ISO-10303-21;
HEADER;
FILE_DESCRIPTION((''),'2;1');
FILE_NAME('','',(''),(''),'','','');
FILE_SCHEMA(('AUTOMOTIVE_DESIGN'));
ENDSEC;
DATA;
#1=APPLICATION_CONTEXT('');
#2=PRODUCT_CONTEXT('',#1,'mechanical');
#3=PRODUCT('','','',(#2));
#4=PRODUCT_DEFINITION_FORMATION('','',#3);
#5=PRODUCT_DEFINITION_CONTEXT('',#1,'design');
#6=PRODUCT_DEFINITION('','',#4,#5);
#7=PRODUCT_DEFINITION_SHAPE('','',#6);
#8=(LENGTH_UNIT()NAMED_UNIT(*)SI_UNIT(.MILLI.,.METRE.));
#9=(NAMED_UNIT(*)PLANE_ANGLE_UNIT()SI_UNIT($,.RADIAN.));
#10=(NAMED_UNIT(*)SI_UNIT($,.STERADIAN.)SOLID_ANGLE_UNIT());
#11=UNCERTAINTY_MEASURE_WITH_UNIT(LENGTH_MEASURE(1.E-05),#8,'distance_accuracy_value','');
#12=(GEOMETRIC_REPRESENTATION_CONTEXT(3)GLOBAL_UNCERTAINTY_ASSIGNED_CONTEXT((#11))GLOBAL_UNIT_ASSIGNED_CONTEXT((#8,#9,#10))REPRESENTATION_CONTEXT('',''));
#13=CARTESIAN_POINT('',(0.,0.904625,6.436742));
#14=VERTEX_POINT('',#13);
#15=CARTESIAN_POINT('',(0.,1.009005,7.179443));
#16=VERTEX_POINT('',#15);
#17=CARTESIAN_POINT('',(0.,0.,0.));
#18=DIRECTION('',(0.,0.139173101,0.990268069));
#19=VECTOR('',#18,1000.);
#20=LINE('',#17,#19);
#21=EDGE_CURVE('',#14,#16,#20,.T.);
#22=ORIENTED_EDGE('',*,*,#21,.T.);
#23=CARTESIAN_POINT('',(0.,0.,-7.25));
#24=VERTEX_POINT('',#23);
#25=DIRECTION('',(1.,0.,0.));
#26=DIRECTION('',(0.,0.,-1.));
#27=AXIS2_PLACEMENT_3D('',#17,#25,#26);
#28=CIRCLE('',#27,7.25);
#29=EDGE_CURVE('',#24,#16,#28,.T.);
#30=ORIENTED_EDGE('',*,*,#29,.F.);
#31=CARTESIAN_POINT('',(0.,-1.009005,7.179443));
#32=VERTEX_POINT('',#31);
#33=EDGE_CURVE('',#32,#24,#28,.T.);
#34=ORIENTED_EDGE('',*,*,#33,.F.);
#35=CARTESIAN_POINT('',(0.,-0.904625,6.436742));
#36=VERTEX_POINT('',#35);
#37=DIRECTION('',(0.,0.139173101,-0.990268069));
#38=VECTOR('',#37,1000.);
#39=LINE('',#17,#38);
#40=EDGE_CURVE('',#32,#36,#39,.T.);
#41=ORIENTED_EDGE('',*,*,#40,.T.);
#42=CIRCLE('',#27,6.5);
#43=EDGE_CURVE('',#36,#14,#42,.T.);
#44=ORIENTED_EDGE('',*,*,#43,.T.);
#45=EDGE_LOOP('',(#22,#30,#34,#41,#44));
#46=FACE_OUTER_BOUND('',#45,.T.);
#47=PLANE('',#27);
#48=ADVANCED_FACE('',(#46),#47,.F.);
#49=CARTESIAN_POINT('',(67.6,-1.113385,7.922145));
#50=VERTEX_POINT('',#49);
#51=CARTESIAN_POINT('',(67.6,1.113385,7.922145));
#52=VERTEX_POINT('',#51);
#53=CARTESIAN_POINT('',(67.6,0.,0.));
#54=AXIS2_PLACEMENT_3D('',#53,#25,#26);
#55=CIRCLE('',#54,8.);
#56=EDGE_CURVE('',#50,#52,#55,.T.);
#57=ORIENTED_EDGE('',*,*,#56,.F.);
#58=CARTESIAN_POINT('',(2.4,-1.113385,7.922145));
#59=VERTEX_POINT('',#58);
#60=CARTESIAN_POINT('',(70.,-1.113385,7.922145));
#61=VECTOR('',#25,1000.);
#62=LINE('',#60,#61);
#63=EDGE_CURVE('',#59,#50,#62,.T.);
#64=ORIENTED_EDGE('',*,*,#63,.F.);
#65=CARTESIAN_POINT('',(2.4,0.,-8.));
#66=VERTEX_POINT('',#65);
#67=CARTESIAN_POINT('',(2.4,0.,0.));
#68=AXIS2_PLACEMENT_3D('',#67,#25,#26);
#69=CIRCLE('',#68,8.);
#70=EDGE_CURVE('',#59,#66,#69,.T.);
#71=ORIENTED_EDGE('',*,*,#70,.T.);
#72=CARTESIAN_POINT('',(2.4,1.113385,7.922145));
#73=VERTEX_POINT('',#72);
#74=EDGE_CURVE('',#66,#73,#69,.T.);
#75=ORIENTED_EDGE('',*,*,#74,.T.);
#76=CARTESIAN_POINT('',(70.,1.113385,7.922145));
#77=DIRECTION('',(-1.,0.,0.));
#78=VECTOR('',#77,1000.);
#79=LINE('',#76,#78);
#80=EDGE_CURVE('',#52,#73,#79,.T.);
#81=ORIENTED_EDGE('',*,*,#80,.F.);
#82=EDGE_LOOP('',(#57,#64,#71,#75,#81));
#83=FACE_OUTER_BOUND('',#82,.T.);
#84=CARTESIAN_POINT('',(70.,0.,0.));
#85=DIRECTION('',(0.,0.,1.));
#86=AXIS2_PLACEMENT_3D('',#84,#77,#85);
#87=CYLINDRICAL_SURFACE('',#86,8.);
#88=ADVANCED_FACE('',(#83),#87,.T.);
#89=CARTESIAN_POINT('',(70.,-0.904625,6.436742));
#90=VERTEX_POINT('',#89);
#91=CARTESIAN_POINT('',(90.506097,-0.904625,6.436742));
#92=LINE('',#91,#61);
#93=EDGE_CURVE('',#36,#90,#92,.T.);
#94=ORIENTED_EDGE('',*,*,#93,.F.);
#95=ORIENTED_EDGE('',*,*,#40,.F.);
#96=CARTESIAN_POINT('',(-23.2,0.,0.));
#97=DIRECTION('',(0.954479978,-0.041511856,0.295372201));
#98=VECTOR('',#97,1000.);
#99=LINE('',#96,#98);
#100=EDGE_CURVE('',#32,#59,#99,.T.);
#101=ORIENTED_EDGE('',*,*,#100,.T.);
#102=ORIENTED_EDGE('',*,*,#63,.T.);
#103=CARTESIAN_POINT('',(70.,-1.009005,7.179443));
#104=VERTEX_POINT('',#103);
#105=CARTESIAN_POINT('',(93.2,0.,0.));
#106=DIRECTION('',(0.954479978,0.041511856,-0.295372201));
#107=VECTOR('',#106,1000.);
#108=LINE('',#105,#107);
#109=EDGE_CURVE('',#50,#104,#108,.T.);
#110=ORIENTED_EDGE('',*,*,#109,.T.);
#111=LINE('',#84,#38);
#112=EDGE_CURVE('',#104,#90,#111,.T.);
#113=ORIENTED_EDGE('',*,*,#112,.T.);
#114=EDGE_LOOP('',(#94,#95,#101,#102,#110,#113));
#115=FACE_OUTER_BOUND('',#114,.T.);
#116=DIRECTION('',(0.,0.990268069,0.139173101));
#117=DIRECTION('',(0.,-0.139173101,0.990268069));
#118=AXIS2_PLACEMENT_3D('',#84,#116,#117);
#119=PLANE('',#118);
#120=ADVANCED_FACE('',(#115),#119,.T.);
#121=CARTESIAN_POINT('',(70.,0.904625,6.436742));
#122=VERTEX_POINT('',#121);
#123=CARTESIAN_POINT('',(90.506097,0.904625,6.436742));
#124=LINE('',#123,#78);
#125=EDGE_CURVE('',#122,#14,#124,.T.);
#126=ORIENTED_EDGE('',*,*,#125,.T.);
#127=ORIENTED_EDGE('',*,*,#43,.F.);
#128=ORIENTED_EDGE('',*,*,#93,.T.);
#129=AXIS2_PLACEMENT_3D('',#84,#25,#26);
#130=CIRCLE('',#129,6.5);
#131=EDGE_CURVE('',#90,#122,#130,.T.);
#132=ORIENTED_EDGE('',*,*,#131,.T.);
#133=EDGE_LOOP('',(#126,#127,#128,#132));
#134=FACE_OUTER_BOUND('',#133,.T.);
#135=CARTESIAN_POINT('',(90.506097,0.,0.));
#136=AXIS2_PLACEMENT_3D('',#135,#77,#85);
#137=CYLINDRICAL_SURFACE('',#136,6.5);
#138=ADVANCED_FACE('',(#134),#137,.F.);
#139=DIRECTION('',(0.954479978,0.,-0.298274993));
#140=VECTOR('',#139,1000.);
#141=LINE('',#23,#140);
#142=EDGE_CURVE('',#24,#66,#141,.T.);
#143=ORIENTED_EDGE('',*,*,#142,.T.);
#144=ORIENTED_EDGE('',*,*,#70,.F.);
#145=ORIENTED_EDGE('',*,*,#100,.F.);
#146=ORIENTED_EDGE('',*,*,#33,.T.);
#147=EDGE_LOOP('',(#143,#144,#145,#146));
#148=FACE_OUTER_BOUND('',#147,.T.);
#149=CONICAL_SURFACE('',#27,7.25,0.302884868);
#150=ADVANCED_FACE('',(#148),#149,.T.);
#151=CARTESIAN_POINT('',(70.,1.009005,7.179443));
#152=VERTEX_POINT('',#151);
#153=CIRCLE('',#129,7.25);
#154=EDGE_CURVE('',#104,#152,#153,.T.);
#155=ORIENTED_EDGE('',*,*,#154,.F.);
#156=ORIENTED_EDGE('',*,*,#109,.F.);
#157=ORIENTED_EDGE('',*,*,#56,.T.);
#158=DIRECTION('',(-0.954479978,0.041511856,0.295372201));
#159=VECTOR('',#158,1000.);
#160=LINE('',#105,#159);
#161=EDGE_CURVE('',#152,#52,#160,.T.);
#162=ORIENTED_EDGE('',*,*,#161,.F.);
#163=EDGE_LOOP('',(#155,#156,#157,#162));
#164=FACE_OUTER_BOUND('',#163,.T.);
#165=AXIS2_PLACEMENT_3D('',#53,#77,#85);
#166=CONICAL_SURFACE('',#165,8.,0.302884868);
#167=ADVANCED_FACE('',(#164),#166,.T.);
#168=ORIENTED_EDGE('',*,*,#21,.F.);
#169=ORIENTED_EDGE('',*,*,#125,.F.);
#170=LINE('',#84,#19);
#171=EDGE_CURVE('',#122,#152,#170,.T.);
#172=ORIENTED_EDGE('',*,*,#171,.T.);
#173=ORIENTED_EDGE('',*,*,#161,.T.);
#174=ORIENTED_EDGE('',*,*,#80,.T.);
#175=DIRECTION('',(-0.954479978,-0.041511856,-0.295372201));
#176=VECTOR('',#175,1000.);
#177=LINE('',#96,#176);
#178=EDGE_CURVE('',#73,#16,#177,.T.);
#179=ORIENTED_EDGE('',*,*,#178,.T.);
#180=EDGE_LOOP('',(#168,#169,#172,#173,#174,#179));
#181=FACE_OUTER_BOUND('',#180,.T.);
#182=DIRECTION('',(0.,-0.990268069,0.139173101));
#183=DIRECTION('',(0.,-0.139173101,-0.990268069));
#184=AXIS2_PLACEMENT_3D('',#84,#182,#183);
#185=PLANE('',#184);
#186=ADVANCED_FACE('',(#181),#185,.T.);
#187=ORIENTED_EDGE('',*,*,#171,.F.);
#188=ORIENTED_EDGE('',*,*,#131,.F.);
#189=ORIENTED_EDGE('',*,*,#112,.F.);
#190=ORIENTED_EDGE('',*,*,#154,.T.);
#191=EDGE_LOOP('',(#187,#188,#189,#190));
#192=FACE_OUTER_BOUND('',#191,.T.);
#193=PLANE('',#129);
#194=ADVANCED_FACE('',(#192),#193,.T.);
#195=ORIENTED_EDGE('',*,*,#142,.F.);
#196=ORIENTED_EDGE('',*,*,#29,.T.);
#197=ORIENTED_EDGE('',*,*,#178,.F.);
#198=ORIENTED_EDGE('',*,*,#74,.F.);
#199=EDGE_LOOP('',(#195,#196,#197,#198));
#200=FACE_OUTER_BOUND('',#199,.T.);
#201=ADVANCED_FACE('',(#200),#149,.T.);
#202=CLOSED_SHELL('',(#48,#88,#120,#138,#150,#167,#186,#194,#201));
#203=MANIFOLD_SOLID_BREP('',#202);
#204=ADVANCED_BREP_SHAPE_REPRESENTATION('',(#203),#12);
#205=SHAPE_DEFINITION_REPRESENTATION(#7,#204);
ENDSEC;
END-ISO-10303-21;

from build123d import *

# Parameters (mm, degrees)
SKETCH1_R          = 8
SKETCH1_R_2        = 7.25
BASE_EXTRUDE_DEPTH = 70
SKETCH2_R          = 7.25
SKETCH2_R_2        = 6.5
EXTRUDE2_DEPTH     = 70
GAP_DEPTH          = 71.908391605


with BuildPart() as part:
    # Sketch1 → Base-Extrude (new body)
    with BuildSketch(Plane(origin=(0, 0, 0), x_dir=(0, 0, -1), z_dir=(1, 0, 0))):
        Circle(SKETCH1_R)
        Circle(SKETCH1_R_2, mode=Mode.SUBTRACT)
    extrude(amount=BASE_EXTRUDE_DEPTH)

    # Sketch2 → Extrude2 (add)
    with BuildSketch(Plane(origin=(0, 0, 0), x_dir=(0, 0, -1), z_dir=(1, 0, 0))):
        Circle(SKETCH2_R)
        Circle(SKETCH2_R_2, mode=Mode.SUBTRACT)
    extrude(amount=EXTRUDE2_DEPTH)

    # Sketch3 → Cut-Revolve1 (revolve, cut)
    with BuildSketch(Plane.XY, mode=Mode.PRIVATE) as cut_revolve1_sk:
        Polygon((70, 8), (70, 7.25), (67.6, 8), align=None)
        Polygon((2.4, 8), (0, 7.25), (0, 8), align=None)
    revolve(cut_revolve1_sk.sketch.rotate(Axis((35, 0, 0), (-1, 0, 0)), 90), axis=Axis((35, 0, 0), (-1, 0, 0)), mode=Mode.SUBTRACT)

    # Sketch4 → Gap (cut, through all)
    with BuildSketch(Plane(origin=(0, 0, 0), x_dir=(0, 0, -1), z_dir=(1, 0, 0))):
        Polygon((0, 0), (-8.1, 1.138380761), (-8.1, -1.138380761), align=None)
    extrude(amount=GAP_DEPTH, mode=Mode.SUBTRACT)


solid = part.part
